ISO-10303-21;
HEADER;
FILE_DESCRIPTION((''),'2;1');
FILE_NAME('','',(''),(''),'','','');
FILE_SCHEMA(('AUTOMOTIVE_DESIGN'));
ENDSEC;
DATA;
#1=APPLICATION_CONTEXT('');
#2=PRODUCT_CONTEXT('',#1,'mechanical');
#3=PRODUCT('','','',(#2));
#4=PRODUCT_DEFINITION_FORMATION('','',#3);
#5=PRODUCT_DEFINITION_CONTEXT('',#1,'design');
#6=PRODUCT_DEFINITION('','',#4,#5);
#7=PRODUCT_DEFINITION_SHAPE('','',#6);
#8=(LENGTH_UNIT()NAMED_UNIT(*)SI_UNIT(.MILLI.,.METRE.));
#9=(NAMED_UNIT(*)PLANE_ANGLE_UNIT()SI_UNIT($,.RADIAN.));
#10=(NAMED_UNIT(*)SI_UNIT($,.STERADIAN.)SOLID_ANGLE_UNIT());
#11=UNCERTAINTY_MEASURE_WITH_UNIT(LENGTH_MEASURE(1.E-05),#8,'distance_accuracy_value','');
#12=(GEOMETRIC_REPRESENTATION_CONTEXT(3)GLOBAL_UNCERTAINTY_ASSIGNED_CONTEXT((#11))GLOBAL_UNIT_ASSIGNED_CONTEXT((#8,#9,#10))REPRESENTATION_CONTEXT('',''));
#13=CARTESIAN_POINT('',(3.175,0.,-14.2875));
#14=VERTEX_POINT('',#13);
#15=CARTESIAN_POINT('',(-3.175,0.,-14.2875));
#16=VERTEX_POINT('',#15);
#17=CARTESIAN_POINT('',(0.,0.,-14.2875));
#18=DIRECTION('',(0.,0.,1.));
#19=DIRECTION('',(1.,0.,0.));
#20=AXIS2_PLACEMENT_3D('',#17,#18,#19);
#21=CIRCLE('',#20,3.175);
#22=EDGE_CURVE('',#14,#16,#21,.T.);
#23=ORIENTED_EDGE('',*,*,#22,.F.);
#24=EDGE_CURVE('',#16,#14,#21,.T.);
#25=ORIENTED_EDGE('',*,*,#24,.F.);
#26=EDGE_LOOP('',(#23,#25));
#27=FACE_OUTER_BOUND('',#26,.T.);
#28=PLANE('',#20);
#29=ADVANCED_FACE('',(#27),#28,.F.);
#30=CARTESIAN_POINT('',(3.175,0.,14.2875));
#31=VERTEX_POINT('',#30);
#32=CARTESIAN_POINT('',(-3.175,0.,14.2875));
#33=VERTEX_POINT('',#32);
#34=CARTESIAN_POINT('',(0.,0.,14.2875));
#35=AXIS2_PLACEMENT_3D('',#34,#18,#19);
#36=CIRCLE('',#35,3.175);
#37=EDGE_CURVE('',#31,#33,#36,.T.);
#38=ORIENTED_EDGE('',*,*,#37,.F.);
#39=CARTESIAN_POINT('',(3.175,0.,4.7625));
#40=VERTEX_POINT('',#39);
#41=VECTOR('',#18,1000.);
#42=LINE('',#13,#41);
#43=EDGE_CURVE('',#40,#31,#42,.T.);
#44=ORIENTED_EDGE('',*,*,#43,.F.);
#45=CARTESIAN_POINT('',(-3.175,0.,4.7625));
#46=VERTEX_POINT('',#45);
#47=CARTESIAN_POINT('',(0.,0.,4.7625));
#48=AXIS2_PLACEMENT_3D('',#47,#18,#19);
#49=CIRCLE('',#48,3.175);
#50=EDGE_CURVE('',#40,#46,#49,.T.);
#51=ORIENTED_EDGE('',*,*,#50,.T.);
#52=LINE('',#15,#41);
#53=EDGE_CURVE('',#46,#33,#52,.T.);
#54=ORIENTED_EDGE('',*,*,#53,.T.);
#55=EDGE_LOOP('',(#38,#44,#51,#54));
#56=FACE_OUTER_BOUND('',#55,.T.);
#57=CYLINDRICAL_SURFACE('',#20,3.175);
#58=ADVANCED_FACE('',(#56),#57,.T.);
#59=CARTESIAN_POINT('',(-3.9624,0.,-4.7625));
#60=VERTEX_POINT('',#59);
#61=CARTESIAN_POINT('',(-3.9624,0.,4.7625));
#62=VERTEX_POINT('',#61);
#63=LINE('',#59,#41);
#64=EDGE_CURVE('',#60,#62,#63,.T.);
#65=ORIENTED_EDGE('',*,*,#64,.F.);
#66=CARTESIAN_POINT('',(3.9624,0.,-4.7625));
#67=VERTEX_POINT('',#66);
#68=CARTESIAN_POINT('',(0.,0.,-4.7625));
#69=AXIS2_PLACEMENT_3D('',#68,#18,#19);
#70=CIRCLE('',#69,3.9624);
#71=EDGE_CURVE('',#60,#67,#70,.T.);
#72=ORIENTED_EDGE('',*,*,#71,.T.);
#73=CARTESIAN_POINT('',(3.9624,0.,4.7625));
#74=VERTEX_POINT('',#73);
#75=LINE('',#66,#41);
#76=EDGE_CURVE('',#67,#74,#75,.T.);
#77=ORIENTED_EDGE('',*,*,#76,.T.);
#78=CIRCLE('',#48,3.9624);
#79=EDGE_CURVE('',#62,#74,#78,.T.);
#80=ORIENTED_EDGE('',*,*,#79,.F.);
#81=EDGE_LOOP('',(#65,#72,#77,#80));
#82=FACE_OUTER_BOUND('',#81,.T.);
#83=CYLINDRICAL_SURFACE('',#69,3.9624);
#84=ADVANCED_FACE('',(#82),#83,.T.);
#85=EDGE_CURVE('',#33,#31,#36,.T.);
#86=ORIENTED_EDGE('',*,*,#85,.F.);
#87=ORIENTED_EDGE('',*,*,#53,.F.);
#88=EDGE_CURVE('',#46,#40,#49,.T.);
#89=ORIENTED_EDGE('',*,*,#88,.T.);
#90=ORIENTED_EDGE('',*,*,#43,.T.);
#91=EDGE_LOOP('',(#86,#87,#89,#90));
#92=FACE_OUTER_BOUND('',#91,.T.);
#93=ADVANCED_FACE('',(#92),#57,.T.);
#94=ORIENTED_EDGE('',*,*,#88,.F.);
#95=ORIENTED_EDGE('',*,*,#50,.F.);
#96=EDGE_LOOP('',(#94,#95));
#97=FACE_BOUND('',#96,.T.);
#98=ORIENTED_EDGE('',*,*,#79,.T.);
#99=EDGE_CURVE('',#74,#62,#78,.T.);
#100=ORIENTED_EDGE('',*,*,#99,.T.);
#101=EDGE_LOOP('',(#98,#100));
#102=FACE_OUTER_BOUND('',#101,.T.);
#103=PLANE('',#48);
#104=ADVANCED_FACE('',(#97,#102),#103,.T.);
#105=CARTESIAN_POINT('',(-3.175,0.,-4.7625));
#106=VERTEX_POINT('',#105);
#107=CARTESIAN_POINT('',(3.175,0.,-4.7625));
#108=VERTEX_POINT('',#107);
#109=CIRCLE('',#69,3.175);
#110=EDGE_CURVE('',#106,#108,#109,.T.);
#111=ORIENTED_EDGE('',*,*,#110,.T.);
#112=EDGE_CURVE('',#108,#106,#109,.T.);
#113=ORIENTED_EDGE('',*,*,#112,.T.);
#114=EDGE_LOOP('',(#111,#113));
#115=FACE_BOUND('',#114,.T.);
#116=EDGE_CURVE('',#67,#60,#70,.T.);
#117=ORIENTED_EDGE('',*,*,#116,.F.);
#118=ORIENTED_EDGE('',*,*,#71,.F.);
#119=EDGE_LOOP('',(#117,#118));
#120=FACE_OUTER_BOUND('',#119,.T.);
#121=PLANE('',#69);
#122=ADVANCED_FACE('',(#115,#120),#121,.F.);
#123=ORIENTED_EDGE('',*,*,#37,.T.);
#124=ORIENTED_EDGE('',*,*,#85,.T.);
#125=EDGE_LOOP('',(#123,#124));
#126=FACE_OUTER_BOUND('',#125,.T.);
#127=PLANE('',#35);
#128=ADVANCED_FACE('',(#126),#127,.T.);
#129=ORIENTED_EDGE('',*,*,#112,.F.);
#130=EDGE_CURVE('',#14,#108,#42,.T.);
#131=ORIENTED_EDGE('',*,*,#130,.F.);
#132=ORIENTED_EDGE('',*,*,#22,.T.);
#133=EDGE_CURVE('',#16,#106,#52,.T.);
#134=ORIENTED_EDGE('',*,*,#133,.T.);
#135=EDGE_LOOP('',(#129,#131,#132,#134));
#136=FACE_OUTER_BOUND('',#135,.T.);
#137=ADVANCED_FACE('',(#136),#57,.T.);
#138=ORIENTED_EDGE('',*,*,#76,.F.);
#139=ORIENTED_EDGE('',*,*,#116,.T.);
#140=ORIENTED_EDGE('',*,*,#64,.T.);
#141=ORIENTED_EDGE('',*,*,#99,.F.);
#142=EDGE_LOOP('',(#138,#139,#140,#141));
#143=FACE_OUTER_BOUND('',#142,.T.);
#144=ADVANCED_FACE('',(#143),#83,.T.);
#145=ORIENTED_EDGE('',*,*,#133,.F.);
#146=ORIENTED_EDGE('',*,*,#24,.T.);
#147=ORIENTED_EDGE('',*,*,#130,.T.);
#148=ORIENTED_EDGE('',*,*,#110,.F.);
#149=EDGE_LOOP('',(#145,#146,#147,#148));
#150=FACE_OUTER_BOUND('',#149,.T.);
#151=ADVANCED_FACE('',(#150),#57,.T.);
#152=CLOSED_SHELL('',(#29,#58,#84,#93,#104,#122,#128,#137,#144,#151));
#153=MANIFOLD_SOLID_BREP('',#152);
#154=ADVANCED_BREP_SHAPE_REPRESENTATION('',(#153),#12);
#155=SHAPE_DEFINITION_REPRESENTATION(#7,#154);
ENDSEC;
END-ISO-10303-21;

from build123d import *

# Parameters (mm, degrees)
BOSS_EXTRUDE1_DEPTH      = 4.7625
BOSS_EXTRUDE1_DEPTH_BACK = 4.7625
SKETCH1_R                = 3.9624
BOSS_EXTRUDE2_DEPTH      = 14.2875
BOSS_EXTRUDE2_DEPTH_BACK = 14.2875
BOSS_EXTRUDE2_START      = -4.7625
SKETCH2_R                = 3.175


with BuildPart() as part:
    # Sketch1 → Boss-Extrude1 (new, two sides: drawn at the far end of the back side and taken through both)
    with BuildSketch(Plane.XY.offset(-BOSS_EXTRUDE1_DEPTH_BACK)):
        Circle(SKETCH1_R)
    extrude(amount=BOSS_EXTRUDE1_DEPTH + BOSS_EXTRUDE1_DEPTH_BACK)

    # Sketch2 → Boss-Extrude2 (add, two sides: drawn at the far end of the back side and taken through both)
    with BuildSketch(Plane.XY.offset(4.7625).offset(BOSS_EXTRUDE2_START - BOSS_EXTRUDE2_DEPTH_BACK)):
        Circle(SKETCH2_R)
    extrude(amount=BOSS_EXTRUDE2_DEPTH + BOSS_EXTRUDE2_DEPTH_BACK)


solid = part.part
